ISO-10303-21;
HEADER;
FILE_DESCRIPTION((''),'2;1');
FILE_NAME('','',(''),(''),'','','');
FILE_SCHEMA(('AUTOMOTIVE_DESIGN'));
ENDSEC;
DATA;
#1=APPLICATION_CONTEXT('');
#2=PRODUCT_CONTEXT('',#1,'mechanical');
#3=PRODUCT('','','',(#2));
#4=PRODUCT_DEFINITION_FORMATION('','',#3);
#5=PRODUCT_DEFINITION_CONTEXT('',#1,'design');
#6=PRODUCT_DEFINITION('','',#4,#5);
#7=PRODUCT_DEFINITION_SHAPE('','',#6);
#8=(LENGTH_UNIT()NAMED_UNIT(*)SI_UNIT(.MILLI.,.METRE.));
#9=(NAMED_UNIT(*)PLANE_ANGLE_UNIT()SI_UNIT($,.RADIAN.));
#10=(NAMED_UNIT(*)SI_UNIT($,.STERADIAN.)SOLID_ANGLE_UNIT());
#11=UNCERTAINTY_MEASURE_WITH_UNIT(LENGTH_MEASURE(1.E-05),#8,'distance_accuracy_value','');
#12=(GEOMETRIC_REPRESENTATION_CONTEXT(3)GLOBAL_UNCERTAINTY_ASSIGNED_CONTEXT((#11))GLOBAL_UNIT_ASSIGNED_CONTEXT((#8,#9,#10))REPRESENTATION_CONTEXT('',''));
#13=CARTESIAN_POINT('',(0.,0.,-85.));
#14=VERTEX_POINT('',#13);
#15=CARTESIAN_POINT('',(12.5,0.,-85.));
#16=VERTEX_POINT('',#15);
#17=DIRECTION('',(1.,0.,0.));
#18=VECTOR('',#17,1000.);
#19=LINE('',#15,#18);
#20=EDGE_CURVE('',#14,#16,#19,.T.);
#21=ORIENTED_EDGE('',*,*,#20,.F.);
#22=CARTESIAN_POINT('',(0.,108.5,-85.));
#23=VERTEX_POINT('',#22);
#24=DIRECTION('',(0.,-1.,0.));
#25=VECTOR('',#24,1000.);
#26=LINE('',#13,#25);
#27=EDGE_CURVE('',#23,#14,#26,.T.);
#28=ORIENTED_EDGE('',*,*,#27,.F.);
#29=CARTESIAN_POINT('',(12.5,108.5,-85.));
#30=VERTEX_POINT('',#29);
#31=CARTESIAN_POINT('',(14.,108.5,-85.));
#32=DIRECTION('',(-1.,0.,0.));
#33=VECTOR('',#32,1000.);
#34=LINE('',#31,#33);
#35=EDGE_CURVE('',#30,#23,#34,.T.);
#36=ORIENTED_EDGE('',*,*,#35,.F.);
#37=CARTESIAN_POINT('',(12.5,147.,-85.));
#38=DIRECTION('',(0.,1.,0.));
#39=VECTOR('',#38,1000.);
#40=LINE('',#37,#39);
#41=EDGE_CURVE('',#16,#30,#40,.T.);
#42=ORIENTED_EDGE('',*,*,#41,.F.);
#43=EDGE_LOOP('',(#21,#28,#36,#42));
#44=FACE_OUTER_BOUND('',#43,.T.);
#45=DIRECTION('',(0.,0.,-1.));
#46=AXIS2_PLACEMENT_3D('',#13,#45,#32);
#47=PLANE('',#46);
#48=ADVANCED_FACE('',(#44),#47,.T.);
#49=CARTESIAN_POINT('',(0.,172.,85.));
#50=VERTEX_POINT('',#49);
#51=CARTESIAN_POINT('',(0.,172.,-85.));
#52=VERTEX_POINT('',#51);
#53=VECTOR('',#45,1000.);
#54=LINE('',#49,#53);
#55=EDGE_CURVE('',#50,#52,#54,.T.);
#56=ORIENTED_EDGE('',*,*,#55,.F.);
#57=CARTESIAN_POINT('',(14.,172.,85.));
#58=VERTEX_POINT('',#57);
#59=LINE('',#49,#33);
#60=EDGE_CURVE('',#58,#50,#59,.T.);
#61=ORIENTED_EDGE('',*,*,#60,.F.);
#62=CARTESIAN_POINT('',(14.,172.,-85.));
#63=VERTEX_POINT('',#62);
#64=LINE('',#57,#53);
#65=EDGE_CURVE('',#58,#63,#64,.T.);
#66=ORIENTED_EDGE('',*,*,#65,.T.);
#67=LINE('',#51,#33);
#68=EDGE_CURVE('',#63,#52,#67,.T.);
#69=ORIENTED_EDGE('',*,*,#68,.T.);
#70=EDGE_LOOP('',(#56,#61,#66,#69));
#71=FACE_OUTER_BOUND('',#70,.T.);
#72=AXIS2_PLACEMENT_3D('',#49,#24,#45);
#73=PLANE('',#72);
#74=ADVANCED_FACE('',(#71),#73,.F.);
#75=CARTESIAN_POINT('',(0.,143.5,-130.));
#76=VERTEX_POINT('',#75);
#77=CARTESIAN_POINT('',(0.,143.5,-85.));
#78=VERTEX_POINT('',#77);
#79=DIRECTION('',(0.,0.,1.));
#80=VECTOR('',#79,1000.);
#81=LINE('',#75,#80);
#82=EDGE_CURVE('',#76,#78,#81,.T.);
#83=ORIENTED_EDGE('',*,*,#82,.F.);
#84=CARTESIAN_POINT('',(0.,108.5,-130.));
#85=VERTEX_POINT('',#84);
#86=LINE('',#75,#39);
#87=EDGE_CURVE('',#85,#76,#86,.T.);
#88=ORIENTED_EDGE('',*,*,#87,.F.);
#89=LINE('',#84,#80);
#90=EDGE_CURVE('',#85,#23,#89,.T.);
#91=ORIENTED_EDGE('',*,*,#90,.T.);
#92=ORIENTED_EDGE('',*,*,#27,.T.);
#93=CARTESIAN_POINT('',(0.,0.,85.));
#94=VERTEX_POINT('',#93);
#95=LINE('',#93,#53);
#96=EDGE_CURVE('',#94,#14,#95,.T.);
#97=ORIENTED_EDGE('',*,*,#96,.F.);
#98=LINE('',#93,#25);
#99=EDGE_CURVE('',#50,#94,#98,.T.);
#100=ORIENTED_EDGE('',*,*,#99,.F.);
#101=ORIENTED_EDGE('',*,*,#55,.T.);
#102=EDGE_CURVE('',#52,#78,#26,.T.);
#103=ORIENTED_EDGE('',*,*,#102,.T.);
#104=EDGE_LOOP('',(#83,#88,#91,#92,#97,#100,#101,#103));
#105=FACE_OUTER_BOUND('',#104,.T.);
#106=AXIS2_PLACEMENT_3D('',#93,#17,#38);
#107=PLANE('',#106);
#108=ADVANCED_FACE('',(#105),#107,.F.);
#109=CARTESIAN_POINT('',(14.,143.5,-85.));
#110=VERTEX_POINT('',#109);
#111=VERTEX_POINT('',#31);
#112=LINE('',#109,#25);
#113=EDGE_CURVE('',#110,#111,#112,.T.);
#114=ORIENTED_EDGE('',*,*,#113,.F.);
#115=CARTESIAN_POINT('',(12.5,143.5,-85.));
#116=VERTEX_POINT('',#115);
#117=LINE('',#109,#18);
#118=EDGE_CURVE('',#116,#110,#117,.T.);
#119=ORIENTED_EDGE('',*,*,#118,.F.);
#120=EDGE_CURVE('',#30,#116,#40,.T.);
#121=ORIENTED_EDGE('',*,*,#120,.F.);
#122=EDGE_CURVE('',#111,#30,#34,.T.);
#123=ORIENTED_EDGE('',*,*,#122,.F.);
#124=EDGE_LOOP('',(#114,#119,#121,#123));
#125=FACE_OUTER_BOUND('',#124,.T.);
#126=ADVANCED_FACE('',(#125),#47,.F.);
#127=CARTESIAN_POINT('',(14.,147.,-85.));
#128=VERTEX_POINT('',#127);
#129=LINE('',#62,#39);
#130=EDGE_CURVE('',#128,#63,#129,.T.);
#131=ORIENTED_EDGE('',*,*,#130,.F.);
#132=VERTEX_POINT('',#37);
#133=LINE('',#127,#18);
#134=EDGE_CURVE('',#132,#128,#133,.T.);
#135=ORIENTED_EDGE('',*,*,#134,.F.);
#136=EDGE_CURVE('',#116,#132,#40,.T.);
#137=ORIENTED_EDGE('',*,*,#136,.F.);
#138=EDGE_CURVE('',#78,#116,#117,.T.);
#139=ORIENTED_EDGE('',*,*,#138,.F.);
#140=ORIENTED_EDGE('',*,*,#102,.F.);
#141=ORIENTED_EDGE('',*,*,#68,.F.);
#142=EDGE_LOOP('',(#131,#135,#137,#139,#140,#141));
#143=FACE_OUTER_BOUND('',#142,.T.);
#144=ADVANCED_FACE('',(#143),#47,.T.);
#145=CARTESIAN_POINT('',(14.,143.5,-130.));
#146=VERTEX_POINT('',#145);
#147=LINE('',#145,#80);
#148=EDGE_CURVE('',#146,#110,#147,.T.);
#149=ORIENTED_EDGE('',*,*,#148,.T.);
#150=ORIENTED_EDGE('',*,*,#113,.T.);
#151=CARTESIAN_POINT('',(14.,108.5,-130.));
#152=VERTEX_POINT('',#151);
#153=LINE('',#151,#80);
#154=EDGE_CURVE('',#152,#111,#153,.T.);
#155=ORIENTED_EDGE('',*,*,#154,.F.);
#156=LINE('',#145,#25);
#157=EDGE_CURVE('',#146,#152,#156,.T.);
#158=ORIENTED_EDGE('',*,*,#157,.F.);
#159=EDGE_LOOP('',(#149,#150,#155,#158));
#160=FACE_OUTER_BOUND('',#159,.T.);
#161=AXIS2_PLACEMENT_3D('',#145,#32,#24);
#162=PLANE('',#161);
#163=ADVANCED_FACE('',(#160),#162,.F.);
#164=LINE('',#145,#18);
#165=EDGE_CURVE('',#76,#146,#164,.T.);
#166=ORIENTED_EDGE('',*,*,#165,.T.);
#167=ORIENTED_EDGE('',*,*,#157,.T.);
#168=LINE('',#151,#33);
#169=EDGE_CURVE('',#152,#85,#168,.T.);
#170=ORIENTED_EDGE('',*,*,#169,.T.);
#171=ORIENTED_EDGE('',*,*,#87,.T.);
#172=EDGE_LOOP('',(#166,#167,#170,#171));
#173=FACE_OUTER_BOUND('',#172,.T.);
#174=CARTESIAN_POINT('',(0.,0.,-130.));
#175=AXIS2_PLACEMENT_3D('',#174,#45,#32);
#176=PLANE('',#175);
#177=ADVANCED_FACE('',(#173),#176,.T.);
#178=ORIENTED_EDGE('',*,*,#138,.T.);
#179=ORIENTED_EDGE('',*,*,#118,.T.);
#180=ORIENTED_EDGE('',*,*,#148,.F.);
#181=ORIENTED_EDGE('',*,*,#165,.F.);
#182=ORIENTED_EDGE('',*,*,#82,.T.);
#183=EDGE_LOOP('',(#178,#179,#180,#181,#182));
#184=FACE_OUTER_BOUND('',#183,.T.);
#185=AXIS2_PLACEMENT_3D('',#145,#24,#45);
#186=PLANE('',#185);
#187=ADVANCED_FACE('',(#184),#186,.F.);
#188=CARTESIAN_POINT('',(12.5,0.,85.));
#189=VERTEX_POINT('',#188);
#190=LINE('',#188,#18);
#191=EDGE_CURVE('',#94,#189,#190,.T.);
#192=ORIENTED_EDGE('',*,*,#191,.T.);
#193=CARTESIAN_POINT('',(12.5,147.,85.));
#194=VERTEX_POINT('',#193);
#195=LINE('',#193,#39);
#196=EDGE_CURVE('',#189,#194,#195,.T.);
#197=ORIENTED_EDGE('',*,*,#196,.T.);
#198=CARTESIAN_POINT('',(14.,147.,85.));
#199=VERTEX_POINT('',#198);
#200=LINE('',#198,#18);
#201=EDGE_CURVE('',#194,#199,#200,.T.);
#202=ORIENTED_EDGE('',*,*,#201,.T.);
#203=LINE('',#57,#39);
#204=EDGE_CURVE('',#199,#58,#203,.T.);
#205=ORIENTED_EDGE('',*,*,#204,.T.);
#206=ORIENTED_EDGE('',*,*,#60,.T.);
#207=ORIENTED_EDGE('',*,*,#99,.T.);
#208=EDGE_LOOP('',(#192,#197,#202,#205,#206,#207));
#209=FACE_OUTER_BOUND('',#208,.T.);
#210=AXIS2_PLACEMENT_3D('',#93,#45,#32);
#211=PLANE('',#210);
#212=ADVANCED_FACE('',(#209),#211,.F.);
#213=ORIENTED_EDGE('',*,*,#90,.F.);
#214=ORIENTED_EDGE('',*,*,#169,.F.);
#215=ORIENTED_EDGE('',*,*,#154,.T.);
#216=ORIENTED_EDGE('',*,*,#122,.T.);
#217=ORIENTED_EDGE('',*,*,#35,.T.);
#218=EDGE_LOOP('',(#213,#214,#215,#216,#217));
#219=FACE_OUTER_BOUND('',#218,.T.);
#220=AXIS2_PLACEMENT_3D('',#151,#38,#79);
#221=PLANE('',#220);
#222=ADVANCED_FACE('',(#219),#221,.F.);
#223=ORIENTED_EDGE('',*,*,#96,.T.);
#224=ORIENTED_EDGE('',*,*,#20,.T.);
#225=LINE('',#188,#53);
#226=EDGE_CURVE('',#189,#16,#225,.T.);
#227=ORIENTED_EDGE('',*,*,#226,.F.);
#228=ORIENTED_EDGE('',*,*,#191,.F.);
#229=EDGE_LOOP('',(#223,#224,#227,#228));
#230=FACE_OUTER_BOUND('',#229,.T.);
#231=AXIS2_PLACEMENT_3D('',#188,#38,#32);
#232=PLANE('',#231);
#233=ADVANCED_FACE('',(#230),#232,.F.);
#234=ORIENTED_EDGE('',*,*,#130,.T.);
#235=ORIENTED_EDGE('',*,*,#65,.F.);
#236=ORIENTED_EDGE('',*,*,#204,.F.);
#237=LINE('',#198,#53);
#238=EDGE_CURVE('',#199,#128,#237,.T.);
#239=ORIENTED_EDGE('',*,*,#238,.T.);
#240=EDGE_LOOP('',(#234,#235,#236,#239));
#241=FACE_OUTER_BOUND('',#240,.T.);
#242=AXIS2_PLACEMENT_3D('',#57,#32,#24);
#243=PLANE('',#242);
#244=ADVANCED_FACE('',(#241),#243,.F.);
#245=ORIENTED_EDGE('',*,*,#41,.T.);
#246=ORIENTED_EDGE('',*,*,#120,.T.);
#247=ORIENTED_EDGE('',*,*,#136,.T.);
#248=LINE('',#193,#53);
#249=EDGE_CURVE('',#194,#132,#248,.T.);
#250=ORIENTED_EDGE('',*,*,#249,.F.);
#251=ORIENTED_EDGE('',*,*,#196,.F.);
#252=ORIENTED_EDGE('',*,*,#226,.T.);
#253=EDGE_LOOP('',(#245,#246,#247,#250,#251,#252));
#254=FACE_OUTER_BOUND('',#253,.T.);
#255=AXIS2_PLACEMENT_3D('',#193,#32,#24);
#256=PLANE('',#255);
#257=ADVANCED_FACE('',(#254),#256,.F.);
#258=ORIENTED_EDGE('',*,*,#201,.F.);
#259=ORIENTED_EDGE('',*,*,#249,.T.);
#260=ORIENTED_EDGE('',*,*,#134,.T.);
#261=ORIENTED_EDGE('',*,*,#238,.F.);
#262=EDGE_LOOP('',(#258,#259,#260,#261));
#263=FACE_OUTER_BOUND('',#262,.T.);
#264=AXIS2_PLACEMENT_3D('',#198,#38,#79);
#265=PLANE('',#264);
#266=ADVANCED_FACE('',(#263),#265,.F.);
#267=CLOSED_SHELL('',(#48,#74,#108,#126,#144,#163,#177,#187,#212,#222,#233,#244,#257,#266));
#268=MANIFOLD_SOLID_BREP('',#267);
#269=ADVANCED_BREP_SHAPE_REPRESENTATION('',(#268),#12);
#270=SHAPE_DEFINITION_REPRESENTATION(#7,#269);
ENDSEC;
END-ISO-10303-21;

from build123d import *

# Parameters (mm, degrees)
EXTRUDE_1_DEPTH = 85
SKETCH_4_W      = 14
SKETCH_4_H      = 35
EXTRUDE_2_DEPTH = 45


with BuildPart() as part:
    # 草图1 → 凸台-拉伸1 (new, symmetric)
    with BuildSketch(Plane.XY):
        Polygon((0, 0), (0, 172), (14, 172), (14, 147), (12.5, 147), (12.5, 0), align=None)
    extrude(amount=EXTRUDE_1_DEPTH, both=True)

    # 草图4 → 凸台-拉伸2 (add)
    with BuildSketch(Plane(origin=(0, 0, -85), x_dir=(-1, 0, 0), z_dir=(0, 0, -1))):
        with Locations((-7, 126)):
            Rectangle(SKETCH_4_W, SKETCH_4_H)
    extrude(amount=EXTRUDE_2_DEPTH)


solid = part.part
